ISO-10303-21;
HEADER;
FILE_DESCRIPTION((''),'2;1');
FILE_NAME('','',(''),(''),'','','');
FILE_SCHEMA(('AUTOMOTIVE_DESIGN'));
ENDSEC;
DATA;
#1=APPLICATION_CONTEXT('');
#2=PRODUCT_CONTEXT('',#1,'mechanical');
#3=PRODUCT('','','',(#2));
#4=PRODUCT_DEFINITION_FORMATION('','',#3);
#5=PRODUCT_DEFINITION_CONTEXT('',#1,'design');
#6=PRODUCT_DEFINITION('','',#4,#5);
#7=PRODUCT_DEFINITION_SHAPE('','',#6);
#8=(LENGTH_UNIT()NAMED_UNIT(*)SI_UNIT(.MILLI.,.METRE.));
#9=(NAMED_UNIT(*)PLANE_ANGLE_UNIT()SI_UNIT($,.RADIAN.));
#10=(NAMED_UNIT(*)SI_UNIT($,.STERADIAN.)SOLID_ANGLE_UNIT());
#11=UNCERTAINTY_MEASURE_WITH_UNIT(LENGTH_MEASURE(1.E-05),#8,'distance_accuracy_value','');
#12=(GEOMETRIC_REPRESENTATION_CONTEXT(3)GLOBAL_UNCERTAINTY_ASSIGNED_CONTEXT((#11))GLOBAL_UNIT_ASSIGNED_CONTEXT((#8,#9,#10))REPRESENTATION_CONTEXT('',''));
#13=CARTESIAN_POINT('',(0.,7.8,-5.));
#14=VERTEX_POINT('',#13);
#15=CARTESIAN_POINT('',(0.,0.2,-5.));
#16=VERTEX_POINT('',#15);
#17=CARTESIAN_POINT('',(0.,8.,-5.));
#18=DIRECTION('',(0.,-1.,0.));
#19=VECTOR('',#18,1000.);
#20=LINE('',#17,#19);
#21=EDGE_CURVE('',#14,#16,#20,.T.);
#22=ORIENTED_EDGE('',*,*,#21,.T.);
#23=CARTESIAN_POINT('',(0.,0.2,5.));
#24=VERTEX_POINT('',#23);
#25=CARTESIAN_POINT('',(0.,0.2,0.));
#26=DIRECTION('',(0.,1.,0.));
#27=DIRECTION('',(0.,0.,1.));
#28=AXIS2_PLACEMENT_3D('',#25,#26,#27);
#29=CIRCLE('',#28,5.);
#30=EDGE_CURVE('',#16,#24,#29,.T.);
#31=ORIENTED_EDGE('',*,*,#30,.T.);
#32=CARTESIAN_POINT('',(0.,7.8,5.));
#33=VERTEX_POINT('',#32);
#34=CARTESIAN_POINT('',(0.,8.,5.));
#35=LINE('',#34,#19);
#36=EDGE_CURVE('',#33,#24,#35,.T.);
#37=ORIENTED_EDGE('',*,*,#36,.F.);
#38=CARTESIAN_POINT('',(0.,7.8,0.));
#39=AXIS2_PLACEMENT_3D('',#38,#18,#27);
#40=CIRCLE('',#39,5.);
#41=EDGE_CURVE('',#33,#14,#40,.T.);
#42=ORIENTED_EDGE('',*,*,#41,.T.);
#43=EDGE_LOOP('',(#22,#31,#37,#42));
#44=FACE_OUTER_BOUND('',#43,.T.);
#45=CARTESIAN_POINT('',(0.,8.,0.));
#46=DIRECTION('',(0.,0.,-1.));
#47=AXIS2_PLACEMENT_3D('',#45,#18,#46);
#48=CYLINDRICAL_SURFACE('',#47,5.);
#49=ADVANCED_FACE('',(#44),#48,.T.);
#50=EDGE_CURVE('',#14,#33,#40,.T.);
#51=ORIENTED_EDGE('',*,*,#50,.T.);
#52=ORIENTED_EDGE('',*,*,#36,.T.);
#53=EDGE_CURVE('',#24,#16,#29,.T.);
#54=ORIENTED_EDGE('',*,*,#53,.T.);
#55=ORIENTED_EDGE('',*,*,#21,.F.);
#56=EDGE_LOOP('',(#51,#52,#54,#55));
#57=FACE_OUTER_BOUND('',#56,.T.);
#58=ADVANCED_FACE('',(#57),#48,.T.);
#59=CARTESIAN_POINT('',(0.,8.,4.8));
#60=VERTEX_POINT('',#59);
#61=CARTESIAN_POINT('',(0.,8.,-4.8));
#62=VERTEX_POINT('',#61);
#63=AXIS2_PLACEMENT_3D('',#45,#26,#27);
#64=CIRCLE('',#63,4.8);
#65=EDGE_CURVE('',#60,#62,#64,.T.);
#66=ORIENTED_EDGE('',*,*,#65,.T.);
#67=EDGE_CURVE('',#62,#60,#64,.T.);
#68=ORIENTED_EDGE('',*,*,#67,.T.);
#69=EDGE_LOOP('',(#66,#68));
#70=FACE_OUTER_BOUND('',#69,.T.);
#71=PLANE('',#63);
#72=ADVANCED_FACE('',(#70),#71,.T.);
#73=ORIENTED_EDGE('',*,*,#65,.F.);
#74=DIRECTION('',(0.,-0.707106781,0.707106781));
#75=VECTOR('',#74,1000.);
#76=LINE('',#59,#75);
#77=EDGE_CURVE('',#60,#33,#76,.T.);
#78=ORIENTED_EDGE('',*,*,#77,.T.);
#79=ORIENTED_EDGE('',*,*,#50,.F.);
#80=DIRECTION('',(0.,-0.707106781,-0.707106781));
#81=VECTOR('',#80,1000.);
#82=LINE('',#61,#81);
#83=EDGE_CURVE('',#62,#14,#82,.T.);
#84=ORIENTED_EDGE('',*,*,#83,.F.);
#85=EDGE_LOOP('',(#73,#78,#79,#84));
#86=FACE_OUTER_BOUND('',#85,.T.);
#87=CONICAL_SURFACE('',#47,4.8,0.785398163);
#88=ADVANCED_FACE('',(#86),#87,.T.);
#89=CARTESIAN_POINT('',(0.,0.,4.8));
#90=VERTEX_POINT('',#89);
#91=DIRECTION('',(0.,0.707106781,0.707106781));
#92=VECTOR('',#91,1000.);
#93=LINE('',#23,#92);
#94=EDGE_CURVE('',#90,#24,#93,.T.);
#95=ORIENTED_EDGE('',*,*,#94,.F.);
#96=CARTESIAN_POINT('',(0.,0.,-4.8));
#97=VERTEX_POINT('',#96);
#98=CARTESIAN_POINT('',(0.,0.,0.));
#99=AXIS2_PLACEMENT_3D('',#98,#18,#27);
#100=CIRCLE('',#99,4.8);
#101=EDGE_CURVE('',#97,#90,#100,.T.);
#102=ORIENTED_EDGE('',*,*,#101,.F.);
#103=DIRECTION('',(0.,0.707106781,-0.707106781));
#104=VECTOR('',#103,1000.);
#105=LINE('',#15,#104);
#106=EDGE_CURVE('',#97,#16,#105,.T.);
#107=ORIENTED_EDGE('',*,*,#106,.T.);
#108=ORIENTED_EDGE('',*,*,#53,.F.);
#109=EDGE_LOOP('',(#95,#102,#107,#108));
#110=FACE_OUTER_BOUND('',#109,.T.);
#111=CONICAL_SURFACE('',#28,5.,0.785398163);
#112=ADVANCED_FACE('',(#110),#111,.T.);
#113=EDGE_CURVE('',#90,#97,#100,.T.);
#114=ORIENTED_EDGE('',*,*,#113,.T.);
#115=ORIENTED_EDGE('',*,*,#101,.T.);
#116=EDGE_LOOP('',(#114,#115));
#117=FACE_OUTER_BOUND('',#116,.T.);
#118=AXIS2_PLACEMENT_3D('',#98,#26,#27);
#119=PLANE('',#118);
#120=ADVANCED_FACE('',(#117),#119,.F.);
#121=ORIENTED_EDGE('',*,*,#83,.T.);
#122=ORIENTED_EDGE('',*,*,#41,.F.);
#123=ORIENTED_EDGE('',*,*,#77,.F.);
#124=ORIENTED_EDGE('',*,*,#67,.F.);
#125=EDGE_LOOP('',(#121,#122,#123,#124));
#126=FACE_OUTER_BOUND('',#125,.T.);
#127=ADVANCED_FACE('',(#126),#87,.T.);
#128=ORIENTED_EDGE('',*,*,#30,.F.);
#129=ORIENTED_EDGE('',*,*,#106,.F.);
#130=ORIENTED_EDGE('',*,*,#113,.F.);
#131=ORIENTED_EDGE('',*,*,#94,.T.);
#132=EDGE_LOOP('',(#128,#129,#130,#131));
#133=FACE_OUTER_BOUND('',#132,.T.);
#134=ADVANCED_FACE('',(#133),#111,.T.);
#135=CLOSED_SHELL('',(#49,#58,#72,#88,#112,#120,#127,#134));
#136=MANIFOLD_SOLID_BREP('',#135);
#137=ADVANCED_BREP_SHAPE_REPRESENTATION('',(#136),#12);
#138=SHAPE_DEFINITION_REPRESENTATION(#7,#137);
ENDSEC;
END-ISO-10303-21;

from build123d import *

# Parameters (mm, degrees)
SKETCH1_R           = 5
BOSS_EXTRUDE1_DEPTH = 8
CHAMFER1_SIZE       = 0.2


with BuildPart() as part:
    # Sketch1 → Boss-Extrude1 (new body)
    with BuildSketch(Plane(origin=(0, 0, 0), x_dir=(1, 0, 0), z_dir=(0, 1, 0))):
        with Locations(Location((0, 0, 0), (0, 0, 270))):
            Circle(SKETCH1_R)
    extrude(amount=BOSS_EXTRUDE1_DEPTH)

    # Chamfer1
    chamfer1_edges = [part.edges().sort_by_distance(p)[0] for p in [
        (0, 0, -5),
        (0, 8, -5),
    ]]
    chamfer(chamfer1_edges, length=CHAMFER1_SIZE)


solid = part.part
